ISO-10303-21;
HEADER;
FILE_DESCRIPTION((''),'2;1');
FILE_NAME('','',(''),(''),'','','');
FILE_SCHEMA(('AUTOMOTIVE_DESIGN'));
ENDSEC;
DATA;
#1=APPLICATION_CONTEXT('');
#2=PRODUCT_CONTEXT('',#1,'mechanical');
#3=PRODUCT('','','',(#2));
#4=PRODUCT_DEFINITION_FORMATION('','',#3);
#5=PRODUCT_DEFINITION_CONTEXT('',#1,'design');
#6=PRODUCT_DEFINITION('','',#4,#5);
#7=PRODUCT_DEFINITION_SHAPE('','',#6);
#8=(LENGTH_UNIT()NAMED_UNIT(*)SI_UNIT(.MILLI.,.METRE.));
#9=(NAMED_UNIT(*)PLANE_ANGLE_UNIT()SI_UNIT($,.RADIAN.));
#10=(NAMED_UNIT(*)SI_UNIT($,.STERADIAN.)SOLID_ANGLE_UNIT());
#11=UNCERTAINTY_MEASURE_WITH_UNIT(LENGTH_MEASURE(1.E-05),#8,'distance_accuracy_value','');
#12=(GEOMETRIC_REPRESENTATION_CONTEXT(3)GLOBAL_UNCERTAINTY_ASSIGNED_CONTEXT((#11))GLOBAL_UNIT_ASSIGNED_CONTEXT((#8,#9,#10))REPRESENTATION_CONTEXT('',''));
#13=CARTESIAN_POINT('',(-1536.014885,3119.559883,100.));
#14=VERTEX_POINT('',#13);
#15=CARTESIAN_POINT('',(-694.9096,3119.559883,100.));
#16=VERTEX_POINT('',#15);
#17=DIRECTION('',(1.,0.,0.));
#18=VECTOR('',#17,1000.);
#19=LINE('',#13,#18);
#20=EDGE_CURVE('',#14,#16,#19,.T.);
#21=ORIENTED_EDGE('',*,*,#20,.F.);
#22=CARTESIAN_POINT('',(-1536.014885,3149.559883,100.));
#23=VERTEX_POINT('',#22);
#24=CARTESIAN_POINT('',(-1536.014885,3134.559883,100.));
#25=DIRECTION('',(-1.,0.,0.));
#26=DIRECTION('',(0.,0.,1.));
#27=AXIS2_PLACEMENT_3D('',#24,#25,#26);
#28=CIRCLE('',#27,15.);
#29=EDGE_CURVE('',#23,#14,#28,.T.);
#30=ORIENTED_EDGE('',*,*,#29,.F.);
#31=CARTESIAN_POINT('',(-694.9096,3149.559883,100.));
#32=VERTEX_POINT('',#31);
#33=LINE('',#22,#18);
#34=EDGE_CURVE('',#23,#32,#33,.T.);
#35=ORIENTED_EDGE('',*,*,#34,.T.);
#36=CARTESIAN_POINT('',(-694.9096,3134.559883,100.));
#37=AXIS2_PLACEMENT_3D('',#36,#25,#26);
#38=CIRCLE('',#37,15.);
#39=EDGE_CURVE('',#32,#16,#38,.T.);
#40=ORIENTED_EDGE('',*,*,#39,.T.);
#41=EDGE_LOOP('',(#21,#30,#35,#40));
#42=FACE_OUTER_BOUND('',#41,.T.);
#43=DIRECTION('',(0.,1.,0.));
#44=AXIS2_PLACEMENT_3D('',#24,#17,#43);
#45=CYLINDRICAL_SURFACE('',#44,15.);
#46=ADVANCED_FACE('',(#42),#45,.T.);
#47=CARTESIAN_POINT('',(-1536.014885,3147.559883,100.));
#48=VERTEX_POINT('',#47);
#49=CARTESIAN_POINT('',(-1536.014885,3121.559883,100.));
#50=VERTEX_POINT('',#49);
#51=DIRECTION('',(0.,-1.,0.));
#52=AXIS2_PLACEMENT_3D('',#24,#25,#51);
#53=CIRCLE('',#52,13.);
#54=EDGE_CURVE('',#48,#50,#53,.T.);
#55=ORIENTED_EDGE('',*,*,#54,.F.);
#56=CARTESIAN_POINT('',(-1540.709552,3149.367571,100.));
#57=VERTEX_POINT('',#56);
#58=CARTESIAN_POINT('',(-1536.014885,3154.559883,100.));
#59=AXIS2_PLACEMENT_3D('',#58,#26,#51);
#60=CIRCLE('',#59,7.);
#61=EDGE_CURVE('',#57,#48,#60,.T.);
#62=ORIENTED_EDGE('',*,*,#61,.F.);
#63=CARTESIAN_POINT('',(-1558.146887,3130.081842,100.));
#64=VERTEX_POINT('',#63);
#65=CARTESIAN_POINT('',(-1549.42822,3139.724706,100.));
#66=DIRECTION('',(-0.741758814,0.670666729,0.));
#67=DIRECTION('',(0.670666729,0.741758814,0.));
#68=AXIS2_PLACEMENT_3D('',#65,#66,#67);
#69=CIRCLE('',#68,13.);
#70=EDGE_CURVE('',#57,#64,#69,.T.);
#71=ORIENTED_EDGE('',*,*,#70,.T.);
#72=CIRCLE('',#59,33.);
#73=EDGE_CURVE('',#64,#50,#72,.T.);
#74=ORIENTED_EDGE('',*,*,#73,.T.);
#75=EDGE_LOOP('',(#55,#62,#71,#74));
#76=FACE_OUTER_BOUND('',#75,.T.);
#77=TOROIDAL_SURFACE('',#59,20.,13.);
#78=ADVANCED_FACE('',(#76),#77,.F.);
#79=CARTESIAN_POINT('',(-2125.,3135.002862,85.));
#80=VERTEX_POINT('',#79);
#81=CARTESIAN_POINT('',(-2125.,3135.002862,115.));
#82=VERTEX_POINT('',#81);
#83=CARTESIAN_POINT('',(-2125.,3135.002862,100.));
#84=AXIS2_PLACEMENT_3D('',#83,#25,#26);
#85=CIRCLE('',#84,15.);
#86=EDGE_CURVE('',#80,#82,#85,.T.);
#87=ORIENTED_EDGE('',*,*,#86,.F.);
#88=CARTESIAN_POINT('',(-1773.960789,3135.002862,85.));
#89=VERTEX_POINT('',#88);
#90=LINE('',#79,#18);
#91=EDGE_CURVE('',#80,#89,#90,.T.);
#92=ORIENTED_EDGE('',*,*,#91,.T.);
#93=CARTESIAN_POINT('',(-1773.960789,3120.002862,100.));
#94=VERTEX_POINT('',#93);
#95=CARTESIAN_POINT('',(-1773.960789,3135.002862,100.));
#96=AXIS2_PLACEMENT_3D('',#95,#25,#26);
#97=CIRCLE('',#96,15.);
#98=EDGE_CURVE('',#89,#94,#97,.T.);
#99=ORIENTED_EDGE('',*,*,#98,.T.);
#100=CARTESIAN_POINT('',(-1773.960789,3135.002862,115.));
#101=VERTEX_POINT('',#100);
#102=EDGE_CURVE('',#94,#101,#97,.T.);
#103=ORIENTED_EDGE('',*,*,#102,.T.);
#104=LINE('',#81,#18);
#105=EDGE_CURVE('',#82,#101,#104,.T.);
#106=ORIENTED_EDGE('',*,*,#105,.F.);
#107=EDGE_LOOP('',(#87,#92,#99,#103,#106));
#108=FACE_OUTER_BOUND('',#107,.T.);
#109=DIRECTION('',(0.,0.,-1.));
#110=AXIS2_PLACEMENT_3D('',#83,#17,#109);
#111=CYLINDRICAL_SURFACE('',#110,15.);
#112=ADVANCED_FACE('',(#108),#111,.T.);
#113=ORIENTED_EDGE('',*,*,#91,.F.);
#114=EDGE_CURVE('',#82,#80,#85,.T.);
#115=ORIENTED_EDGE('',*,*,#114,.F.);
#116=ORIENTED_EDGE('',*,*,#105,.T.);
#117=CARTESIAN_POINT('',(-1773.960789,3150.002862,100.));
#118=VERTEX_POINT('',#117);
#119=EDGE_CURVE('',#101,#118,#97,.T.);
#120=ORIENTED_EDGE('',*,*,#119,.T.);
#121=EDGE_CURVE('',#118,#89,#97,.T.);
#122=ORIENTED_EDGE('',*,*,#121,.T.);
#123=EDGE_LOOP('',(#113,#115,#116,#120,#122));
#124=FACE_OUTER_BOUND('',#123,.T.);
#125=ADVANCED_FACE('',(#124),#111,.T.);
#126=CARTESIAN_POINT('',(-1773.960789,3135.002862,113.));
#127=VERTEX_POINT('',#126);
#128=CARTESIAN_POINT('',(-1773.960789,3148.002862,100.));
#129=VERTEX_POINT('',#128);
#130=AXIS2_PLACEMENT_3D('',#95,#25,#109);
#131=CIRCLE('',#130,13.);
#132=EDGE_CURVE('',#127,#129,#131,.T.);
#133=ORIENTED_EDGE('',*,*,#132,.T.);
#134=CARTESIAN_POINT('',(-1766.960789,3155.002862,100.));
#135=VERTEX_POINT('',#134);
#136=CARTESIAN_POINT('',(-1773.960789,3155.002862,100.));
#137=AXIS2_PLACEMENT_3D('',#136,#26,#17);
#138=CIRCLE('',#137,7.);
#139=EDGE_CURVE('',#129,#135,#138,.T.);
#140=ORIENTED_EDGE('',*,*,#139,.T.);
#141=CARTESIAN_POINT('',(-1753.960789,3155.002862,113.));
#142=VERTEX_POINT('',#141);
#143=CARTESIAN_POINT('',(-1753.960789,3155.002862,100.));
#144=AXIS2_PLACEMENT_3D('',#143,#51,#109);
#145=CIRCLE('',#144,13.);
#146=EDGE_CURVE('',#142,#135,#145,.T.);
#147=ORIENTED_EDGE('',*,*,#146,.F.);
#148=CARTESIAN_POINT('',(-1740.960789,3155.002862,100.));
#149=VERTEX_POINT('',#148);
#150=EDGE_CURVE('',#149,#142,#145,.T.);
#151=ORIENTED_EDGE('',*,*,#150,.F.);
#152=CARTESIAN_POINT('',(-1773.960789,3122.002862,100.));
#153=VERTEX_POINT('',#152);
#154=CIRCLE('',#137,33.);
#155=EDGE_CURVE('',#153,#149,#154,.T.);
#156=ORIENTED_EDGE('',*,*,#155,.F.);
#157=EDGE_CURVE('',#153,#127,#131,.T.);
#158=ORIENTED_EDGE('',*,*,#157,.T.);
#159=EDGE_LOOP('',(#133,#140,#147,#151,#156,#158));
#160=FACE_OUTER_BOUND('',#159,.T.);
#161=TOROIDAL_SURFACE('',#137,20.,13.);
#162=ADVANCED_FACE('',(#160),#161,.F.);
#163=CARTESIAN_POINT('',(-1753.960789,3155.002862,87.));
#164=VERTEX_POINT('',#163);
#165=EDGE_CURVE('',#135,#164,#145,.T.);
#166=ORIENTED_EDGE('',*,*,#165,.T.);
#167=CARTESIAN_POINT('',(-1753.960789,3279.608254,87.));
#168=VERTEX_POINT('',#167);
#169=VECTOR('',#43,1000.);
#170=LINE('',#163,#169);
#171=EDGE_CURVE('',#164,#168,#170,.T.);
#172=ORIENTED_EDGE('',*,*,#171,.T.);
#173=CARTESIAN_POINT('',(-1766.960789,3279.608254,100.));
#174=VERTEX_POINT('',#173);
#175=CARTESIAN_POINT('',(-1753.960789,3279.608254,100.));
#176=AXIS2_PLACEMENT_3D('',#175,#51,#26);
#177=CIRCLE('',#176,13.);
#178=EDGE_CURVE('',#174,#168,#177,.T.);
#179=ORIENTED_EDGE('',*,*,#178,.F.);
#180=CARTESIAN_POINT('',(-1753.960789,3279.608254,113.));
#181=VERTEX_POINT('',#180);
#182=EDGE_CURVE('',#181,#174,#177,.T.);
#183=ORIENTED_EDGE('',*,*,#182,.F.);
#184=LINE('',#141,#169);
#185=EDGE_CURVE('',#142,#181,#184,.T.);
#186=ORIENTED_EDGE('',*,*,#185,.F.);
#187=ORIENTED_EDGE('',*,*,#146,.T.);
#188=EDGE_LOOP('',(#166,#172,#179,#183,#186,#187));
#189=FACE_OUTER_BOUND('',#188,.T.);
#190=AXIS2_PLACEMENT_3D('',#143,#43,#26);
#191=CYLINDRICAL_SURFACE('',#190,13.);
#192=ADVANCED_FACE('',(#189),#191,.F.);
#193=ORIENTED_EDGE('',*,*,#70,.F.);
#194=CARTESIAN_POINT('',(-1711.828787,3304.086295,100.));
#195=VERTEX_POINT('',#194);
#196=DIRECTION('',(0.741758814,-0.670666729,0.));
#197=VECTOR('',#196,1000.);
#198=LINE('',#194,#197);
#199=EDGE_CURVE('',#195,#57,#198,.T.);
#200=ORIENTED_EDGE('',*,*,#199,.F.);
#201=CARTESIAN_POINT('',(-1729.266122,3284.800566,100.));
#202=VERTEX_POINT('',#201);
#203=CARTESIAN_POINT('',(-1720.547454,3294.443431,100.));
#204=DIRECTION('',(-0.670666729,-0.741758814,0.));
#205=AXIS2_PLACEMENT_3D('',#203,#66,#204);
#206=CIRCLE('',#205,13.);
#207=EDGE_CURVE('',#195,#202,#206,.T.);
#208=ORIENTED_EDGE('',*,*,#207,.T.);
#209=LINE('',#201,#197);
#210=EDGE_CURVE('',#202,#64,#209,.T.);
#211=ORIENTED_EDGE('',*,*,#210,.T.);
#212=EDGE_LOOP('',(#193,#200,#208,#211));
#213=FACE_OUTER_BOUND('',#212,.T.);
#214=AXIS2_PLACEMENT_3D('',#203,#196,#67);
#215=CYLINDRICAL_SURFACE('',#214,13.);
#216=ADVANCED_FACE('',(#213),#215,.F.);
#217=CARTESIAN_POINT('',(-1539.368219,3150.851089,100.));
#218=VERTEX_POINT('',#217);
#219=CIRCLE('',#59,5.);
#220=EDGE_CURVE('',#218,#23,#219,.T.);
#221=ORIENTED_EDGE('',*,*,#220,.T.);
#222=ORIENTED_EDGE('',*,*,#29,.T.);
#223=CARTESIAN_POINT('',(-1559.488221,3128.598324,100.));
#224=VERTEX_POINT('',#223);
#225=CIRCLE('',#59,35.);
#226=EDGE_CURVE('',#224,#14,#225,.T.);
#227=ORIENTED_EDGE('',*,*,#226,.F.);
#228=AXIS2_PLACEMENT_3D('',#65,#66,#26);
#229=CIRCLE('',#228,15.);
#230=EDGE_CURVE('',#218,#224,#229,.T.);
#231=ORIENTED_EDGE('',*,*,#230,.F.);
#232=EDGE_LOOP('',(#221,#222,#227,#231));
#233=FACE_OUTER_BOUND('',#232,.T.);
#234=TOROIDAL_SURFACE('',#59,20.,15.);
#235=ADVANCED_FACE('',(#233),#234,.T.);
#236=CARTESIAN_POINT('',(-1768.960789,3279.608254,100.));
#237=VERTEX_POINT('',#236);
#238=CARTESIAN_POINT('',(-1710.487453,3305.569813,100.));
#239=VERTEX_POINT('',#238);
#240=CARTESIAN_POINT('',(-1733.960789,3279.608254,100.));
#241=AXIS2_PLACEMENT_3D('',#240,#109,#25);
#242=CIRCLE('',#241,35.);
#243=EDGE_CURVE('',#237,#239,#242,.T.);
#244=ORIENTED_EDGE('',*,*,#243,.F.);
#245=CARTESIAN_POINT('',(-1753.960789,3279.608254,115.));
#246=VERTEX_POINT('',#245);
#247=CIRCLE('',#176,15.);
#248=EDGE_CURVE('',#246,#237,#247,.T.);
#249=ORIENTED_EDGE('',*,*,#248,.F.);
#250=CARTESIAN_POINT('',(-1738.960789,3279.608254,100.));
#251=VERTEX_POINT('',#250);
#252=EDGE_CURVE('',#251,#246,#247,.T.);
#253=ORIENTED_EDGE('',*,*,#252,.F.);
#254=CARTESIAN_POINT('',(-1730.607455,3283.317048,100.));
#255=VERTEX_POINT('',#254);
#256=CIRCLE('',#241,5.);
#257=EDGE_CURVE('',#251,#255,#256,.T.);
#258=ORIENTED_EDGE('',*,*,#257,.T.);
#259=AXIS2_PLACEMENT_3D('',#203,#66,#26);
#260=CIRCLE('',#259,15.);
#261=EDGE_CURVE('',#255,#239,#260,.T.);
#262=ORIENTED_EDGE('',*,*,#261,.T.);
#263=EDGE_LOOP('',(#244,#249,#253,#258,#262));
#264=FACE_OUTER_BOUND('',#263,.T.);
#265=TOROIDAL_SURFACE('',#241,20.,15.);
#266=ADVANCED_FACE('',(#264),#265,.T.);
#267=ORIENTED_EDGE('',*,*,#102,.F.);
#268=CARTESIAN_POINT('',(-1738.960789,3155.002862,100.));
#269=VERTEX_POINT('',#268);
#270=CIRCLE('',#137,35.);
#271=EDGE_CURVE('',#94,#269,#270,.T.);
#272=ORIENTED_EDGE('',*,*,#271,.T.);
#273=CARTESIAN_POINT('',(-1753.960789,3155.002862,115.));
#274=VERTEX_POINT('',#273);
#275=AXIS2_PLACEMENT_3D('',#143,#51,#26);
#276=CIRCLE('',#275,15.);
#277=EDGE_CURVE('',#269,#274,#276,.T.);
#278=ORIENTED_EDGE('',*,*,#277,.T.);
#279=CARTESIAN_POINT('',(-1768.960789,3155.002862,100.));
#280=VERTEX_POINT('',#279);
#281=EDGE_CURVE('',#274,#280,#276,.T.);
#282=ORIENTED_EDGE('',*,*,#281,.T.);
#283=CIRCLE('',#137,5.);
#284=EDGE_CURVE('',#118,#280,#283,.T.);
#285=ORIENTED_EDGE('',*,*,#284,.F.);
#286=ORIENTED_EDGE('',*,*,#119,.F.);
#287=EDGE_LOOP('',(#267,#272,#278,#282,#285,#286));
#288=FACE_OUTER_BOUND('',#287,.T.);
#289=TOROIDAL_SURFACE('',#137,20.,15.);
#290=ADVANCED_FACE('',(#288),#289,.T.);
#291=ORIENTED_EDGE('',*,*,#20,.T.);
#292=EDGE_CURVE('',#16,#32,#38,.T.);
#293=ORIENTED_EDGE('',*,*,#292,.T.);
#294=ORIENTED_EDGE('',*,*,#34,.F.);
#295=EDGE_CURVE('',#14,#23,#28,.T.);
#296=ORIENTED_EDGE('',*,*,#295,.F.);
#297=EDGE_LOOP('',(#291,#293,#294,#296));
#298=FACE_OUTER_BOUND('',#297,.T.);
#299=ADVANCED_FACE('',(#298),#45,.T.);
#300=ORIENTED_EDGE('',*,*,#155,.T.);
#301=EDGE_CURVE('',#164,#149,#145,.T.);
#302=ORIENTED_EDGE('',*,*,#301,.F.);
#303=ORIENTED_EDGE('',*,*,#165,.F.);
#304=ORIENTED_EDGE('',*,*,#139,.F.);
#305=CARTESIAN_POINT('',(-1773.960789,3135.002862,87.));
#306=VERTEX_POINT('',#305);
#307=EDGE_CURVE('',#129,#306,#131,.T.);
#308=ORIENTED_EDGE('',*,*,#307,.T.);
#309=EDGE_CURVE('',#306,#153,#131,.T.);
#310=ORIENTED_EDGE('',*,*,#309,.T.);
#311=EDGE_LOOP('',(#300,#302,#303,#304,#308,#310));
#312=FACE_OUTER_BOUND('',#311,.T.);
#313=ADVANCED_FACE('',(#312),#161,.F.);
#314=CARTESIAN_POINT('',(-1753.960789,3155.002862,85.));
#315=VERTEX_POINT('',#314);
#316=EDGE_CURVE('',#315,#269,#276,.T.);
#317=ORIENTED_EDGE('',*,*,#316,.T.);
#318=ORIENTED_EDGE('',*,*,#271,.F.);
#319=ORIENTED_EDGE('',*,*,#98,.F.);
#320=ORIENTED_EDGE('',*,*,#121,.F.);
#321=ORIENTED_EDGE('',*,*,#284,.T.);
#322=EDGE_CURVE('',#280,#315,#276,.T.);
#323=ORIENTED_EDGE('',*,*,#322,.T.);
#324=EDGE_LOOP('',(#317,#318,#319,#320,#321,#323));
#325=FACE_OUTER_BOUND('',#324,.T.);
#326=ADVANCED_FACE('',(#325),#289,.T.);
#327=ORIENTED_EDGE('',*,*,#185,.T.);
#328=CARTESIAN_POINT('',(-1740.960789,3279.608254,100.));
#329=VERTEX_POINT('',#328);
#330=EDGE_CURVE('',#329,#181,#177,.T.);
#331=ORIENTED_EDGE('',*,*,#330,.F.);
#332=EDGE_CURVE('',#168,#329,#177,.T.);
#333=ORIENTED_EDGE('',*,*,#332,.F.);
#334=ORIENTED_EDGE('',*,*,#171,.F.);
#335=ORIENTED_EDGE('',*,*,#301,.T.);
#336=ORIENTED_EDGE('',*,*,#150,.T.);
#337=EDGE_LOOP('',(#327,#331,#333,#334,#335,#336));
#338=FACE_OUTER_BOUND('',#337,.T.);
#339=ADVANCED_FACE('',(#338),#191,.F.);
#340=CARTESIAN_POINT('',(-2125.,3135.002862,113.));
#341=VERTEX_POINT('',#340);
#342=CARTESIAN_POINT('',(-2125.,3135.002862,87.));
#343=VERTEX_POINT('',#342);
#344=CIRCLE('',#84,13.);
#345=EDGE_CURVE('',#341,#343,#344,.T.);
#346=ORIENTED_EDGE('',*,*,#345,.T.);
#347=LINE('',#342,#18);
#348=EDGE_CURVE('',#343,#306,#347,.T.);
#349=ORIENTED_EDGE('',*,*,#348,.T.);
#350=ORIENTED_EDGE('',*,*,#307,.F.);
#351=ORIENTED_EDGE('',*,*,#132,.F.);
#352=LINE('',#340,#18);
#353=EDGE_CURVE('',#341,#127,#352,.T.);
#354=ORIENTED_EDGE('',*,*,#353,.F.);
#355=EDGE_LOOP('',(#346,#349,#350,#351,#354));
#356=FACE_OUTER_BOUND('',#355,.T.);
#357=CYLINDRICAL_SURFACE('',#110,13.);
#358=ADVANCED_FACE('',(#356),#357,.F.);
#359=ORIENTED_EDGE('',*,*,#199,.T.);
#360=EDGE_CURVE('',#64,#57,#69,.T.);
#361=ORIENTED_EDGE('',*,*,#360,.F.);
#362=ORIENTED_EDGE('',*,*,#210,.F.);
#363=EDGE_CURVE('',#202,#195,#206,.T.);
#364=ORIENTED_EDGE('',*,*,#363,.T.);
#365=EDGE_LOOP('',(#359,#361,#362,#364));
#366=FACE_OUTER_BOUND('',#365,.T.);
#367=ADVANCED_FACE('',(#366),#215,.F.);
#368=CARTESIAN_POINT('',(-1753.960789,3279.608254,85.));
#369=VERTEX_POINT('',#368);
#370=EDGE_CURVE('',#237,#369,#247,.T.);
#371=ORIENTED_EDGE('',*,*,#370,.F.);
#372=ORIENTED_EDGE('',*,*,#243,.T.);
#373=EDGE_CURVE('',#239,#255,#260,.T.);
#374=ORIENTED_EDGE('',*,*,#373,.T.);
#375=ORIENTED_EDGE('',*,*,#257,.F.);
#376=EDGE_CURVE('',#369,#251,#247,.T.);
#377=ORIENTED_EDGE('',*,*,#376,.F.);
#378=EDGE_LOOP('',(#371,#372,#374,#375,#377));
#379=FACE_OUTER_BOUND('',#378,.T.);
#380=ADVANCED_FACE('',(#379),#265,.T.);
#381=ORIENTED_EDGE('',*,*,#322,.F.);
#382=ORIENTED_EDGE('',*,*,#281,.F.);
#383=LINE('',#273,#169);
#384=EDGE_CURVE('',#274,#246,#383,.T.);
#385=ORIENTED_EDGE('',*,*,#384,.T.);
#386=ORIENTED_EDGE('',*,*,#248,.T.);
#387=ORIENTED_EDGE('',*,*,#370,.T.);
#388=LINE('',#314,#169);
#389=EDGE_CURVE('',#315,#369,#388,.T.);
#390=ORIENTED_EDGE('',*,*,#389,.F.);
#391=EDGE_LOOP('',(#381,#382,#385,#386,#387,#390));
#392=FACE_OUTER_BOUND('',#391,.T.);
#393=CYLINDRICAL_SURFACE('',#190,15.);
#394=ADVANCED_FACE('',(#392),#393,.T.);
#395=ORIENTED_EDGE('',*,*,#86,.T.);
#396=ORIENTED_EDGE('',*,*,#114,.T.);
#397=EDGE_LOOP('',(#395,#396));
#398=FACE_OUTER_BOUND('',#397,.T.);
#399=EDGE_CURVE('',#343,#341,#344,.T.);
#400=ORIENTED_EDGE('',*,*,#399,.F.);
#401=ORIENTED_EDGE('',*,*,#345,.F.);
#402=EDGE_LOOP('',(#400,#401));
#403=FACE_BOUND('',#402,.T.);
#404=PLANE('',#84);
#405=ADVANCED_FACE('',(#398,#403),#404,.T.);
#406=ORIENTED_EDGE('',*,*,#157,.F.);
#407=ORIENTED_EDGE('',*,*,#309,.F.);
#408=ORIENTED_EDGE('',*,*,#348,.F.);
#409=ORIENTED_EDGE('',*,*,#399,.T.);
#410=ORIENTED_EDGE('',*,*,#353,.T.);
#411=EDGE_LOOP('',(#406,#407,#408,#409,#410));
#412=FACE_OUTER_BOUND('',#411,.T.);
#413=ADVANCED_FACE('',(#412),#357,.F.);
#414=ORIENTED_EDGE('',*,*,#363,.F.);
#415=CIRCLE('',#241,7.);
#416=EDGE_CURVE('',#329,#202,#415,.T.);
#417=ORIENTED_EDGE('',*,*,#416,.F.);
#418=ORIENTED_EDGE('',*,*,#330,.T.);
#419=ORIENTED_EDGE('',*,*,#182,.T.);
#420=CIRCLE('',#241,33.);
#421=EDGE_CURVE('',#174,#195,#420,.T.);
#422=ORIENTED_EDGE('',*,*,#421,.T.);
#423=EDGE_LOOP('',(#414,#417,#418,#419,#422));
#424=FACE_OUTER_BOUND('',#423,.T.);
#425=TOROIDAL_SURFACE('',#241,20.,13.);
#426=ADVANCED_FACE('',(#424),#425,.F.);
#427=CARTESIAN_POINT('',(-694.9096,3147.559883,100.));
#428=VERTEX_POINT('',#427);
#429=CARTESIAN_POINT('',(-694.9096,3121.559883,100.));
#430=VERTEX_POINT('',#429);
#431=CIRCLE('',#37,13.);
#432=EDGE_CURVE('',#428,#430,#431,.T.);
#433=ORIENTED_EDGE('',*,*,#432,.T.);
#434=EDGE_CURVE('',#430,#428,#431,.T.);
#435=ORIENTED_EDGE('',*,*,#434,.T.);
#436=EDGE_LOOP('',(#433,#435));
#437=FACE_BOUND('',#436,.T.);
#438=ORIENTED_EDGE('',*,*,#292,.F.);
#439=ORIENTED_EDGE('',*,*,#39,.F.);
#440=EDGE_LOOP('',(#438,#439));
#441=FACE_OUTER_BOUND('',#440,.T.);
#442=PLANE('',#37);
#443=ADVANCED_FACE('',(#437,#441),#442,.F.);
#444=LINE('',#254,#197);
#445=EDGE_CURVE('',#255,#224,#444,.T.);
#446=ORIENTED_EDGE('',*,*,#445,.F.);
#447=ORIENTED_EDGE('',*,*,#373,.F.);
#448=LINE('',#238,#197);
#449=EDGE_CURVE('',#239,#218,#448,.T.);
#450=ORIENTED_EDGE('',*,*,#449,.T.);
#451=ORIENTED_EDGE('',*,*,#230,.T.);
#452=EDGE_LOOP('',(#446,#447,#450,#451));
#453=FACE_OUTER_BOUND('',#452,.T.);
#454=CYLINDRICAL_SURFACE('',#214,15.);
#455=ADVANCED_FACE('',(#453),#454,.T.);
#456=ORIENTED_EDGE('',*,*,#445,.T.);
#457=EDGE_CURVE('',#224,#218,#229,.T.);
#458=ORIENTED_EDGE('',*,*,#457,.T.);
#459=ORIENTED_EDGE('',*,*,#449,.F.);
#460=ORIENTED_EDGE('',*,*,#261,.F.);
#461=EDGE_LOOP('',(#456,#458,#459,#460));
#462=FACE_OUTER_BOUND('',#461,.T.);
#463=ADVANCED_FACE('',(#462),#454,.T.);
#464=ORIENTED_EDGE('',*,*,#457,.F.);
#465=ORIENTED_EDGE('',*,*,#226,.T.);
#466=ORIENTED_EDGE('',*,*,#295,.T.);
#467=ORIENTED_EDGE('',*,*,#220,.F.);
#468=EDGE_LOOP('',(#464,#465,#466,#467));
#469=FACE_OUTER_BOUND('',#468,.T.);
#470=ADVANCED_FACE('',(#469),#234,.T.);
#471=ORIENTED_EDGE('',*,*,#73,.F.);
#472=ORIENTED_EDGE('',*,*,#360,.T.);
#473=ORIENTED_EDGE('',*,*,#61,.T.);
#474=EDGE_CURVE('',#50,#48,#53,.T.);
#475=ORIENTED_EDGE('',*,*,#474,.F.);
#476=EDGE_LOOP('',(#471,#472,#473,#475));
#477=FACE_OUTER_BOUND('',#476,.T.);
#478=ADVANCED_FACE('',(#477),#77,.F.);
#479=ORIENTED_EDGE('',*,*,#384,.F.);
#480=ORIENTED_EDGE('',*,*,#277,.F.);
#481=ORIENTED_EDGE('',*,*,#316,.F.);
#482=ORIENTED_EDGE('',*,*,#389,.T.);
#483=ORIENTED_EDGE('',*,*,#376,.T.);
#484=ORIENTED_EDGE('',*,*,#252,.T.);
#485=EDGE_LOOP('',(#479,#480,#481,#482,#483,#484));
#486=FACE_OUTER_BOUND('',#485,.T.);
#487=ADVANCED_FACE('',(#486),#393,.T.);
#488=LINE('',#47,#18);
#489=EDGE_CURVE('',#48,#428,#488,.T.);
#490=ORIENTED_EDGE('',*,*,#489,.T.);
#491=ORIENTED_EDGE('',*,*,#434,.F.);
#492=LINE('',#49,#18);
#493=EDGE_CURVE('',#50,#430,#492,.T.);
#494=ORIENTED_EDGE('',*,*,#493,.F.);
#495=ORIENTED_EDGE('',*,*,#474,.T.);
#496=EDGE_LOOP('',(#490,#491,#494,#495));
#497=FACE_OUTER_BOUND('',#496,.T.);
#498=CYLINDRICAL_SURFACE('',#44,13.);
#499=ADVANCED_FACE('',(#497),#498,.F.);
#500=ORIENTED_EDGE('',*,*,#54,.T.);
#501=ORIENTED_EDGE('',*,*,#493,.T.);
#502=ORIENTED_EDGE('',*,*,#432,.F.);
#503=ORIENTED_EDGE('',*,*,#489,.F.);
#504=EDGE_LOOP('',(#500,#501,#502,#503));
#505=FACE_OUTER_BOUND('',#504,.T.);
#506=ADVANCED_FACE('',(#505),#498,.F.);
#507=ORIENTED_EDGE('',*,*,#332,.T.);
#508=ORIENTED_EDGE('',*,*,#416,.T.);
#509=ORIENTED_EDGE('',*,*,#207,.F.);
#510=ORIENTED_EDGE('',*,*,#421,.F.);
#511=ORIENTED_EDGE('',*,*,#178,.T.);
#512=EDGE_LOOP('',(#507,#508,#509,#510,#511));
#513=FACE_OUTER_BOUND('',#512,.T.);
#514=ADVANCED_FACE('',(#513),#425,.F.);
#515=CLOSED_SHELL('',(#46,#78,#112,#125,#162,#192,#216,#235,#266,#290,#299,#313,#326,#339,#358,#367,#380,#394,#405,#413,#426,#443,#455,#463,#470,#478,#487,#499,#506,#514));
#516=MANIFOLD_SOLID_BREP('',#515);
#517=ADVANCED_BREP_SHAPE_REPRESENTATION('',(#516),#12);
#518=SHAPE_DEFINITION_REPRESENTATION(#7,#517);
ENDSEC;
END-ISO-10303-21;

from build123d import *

# Parameters (mm, degrees)
SWEEP_THIN1_PROFILE_R   = 15
SWEEP_THIN1_PROFILE_R_2 = 13


with BuildPart() as part:
    # Sweep-Thin1: sweep along a curve in space
    with BuildLine() as sweep_thin1_path:
        Line((-2125, 3135.002861913, 100.000000001), (-1773.960788665, 3135.002861913, 100.000000001))
        ThreePointArc((-1773.960788665, 3135.002861913, 100.000000001), (-1759.818653041, 3140.860726289, 100.000000001), (-1753.960788665, 3155.002861913, 100.000000001))
        Line((-1753.960788665, 3155.002861913, 100.000000001), (-1753.960788665, 3279.60825422, 100.000000001))
        ThreePointArc((-1753.960788665, 3279.60825422, 100.000000001), (-1742.076616051, 3297.887568918, 100), (-1720.547454081, 3294.443430502, 100))
        Line((-1720.547454081, 3294.443430502, 100), (-1549.428219579, 3139.724706402, 99.999999999))
        ThreePointArc((-1536.014884995, 3134.559882685, 99.999999999), (-1543.201555794, 3135.895698727, 99.999999999), (-1549.428219579, 3139.724706402, 99.999999999))
        Line((-1536.014884995, 3134.559882685, 99.999999999), (-694.909600267, 3134.559882685, 99.999999999))
    # Sweep-Thin1 profile (on start of the path) → Sweep-Thin1 (sweep)
    with BuildSketch(Plane(origin=(-2125, 3135.002861913, 100.000000001), x_dir=(0, 0, 1), z_dir=(1, 0, 0))):
        Circle(SWEEP_THIN1_PROFILE_R)
        Circle(SWEEP_THIN1_PROFILE_R_2, mode=Mode.SUBTRACT)
    sweep(path=sweep_thin1_path.line)


solid = part.part
